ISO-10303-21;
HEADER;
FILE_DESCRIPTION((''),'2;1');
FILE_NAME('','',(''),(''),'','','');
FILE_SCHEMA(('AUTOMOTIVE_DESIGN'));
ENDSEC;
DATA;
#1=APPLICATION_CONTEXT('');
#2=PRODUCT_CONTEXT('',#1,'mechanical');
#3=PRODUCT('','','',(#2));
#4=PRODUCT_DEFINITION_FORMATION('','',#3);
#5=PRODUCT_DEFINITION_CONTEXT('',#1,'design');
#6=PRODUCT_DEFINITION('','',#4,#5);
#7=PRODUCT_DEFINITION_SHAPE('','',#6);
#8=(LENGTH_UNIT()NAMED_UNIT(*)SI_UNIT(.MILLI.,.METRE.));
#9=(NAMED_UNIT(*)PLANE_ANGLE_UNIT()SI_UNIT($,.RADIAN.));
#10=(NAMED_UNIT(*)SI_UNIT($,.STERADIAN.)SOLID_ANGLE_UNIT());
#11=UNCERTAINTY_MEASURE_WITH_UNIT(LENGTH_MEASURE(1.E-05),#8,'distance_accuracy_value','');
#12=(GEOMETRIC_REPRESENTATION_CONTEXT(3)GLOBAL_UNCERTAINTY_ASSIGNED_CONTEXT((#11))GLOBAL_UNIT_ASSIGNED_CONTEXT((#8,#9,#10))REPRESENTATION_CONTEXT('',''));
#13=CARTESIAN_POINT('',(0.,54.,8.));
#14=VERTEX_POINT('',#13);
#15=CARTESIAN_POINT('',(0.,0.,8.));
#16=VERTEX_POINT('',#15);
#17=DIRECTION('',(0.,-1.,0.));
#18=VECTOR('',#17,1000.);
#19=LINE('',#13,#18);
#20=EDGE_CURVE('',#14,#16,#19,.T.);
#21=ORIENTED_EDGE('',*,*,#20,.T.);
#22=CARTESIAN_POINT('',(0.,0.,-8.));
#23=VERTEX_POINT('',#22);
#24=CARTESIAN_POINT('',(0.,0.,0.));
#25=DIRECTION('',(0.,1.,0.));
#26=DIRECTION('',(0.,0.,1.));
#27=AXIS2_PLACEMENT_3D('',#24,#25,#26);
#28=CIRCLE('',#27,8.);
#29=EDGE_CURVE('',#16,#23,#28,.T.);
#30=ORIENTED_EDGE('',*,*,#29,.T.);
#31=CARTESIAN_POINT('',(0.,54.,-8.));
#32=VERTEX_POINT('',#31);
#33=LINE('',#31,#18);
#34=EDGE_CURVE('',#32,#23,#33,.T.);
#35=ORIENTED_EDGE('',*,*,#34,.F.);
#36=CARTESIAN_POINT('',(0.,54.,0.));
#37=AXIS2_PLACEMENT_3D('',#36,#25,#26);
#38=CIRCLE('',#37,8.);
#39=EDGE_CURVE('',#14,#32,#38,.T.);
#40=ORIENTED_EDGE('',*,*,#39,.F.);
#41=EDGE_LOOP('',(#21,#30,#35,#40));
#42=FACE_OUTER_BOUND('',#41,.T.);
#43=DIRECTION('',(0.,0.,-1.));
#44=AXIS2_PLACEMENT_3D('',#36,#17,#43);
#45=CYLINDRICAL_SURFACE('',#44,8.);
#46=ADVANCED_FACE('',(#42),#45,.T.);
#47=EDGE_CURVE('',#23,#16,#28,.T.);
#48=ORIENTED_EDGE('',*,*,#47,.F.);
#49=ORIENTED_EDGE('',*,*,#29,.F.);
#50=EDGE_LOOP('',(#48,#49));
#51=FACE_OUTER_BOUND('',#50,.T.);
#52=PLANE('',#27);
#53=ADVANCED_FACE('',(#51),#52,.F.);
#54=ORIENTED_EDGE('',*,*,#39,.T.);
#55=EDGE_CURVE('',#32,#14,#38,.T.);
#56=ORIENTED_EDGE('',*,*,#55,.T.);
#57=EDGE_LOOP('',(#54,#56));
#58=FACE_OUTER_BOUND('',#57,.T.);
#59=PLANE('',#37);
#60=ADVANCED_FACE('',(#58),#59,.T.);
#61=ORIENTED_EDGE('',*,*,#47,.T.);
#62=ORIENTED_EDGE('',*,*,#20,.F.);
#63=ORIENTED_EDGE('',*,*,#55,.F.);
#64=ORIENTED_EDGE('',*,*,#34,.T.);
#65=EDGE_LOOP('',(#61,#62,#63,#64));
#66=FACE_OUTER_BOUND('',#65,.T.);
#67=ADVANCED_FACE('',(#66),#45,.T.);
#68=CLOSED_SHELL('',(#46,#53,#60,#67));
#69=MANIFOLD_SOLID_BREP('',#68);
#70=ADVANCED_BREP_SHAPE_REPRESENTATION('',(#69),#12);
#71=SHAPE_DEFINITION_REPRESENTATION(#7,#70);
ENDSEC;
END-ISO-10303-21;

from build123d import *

# Parameters (mm, degrees)
SKETCH1_R           = 8
BOSS_EXTRUDE1_DEPTH = 54


with BuildPart() as part:
    # Sketch1 → Boss-Extrude1 (new body)
    with BuildSketch(Plane(origin=(0, 0, 0), x_dir=(1, 0, 0), z_dir=(0, 1, 0))):
        with Locations(Location((0, 0, 0), (0, 0, 270))):
            Circle(SKETCH1_R)
    extrude(amount=BOSS_EXTRUDE1_DEPTH)


solid = part.part
